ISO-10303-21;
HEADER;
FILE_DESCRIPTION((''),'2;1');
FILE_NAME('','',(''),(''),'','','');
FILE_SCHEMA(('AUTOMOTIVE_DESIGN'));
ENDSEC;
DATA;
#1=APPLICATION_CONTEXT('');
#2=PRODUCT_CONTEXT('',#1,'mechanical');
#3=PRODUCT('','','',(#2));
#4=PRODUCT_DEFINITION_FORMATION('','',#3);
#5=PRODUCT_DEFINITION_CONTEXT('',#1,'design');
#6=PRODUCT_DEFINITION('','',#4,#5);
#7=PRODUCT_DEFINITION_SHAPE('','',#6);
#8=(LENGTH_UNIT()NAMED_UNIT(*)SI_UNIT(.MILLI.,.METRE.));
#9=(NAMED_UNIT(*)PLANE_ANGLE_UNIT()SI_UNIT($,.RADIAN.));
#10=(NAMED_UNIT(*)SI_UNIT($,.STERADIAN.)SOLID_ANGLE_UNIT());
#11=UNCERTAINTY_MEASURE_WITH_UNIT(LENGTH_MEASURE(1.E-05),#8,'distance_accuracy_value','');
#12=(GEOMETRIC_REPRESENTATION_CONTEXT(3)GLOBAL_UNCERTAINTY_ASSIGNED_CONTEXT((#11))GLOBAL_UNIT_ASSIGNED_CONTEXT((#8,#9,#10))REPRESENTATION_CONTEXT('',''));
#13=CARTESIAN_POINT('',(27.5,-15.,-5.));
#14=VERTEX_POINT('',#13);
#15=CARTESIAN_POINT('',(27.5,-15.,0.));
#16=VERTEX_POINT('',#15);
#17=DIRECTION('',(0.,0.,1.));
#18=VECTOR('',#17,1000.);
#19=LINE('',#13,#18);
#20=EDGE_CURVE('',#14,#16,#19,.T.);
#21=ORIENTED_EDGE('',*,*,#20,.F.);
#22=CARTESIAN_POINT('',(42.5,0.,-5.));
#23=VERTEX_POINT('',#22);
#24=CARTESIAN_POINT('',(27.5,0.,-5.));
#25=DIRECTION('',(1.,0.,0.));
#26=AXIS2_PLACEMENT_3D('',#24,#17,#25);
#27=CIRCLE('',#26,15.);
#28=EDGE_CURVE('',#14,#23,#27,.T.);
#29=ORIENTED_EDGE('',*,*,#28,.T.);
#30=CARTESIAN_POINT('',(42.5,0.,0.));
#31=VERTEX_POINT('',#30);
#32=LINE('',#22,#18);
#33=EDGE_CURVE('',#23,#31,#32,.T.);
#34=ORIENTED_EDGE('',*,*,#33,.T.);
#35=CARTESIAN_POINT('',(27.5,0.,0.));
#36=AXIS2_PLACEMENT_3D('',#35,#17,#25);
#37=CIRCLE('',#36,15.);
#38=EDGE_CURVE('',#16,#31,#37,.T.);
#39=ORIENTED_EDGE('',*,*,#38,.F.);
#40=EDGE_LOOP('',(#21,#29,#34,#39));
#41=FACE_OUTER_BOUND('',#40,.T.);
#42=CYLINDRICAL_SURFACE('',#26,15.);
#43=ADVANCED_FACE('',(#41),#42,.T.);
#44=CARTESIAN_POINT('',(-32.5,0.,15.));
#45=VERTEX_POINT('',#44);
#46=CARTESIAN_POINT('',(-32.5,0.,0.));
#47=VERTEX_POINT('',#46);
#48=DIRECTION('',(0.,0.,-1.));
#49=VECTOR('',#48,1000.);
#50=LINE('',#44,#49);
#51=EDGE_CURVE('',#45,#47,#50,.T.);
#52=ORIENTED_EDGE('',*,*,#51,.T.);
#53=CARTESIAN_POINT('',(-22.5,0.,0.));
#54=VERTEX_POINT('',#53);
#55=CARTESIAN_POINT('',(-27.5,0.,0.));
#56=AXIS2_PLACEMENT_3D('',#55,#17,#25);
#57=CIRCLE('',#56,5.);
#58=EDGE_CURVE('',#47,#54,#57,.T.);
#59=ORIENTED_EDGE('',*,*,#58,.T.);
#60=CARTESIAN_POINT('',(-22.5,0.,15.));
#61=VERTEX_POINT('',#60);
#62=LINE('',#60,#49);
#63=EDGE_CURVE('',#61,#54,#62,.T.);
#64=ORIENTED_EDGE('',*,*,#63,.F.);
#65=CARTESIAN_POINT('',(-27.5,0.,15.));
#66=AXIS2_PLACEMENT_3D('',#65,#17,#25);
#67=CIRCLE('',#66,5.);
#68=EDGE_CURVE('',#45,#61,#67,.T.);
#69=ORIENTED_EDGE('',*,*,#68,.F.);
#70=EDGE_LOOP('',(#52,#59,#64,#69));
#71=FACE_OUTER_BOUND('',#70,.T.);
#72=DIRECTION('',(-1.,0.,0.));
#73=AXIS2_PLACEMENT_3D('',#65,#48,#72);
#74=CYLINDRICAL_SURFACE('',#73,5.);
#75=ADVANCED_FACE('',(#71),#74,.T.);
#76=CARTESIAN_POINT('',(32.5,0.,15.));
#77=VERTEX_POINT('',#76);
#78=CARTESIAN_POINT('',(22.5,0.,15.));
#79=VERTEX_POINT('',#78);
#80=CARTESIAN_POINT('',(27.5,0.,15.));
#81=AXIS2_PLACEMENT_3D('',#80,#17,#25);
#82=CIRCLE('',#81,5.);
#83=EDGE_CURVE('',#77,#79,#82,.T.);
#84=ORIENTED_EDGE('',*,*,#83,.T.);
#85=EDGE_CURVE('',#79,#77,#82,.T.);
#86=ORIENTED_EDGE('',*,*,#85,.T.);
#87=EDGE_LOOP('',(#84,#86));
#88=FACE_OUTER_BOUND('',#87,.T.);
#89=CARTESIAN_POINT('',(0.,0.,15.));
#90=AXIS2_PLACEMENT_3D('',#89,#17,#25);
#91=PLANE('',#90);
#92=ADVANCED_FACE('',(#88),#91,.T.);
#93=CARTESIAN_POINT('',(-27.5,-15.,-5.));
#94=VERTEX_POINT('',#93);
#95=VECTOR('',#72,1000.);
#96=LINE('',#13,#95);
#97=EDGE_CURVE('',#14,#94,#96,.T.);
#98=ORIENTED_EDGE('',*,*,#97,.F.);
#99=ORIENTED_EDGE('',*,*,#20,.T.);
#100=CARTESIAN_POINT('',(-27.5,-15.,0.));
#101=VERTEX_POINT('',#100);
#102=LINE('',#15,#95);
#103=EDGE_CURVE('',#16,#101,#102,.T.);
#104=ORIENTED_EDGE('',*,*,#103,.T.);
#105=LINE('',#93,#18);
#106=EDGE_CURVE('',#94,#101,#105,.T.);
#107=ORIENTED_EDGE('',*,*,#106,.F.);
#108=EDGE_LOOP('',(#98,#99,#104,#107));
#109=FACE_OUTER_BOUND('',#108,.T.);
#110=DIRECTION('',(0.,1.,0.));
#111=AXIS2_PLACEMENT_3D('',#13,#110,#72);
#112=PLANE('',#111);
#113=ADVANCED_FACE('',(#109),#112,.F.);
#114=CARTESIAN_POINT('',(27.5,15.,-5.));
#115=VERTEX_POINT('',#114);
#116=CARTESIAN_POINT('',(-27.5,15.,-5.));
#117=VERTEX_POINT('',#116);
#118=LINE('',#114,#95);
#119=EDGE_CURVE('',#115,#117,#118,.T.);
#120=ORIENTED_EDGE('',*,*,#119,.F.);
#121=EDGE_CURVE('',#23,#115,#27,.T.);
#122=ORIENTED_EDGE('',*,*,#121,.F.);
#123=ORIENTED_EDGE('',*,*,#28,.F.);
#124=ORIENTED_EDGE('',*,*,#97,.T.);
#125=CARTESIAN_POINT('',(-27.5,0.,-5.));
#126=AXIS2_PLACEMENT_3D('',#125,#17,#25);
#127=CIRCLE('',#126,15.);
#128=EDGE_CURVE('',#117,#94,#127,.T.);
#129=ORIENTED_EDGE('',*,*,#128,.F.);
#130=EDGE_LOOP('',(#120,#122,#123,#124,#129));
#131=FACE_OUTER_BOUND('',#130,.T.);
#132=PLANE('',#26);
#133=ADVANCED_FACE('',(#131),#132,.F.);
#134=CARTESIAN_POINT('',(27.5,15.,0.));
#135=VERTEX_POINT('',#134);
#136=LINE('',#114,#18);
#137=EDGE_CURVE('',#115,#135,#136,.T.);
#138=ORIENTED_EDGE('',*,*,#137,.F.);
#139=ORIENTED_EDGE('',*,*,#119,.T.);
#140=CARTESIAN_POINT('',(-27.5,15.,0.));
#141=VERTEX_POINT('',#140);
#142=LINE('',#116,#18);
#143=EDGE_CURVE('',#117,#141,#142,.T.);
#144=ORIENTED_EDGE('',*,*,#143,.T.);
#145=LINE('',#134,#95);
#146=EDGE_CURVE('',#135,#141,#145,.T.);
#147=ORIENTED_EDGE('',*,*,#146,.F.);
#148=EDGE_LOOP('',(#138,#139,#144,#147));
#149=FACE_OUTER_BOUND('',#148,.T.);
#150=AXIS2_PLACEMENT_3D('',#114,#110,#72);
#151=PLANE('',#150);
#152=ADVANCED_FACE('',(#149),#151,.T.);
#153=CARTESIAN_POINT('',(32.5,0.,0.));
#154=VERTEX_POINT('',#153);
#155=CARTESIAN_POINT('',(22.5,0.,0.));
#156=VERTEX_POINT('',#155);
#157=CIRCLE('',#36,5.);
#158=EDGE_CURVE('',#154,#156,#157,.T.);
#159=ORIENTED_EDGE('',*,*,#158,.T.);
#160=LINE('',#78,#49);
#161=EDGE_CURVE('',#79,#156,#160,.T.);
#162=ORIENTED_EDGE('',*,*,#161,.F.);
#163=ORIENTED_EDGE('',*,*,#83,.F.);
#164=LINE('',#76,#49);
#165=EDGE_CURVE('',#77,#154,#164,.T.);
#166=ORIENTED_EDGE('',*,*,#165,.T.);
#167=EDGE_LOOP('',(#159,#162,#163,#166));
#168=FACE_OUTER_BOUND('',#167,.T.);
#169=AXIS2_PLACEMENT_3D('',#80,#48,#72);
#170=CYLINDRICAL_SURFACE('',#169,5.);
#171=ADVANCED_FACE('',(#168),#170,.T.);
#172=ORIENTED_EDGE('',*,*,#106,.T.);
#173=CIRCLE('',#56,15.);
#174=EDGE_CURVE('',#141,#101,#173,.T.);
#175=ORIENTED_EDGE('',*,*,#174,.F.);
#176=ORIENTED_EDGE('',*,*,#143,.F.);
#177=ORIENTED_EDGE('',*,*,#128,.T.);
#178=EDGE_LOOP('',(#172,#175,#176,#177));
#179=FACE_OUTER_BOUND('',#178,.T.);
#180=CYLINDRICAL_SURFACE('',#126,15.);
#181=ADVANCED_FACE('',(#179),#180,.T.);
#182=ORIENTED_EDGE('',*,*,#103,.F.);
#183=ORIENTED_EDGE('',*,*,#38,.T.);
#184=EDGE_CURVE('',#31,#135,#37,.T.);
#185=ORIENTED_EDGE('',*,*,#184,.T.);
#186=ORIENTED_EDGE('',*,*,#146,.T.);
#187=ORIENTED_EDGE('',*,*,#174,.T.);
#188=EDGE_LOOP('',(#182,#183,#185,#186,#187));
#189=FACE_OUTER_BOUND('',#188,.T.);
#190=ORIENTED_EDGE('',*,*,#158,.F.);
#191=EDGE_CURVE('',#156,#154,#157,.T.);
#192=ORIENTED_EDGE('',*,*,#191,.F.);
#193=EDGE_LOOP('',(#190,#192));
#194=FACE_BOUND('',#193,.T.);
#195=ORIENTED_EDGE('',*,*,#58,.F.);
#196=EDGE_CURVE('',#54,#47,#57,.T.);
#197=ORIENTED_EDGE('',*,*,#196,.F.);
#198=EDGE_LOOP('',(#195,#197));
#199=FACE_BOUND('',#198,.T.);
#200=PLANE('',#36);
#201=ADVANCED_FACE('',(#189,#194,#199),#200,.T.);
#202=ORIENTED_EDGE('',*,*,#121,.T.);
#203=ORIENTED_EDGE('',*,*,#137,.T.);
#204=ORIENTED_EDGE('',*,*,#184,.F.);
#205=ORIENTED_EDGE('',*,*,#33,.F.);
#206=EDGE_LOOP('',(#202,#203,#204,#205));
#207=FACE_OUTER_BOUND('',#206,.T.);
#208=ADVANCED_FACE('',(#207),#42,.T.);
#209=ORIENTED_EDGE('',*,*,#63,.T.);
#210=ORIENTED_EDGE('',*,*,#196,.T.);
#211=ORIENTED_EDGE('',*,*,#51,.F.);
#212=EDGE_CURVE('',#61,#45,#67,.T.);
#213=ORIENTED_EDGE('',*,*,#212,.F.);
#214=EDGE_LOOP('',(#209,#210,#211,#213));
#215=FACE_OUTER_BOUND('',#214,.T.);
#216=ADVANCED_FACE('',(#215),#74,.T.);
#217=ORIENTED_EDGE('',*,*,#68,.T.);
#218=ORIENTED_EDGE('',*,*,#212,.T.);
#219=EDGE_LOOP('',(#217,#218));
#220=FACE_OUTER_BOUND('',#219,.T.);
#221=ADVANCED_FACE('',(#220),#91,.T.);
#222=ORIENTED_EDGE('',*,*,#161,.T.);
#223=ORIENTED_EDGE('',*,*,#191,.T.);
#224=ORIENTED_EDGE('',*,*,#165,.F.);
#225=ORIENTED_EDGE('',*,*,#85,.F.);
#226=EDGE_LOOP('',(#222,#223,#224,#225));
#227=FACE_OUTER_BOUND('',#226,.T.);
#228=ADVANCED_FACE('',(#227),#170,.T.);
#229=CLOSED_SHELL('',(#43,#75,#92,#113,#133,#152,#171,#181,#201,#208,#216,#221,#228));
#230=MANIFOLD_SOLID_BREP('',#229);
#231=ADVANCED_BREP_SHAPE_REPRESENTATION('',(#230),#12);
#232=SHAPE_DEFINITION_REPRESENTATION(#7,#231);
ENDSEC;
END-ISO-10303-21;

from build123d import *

# Parameters (mm, degrees)
LINK_PLATE_DEPTH = 5
SKETCH1_3_R      = 5
PINS_2X_10_DEPTH = 15


with BuildPart() as part:
    # Link Profile Sketch → Link Plate (new body)
    with BuildSketch(Plane.XY):
        with BuildLine():
            Line((27.5, -15), (-27.5, -15))
            ThreePointArc((-27.5, -15), (-42.5, 0), (-27.5, 15))
            Line((-27.5, 15), (27.5, 15))
            ThreePointArc((27.5, 15), (42.5, 0), (27.5, -15))
        make_face()
    extrude(amount=-LINK_PLATE_DEPTH)

    # Sketch1_3 → Pins 2x_10 (add)
    with BuildSketch(Plane.XY):
        with Locations((-27.5, 0)):
            Circle(SKETCH1_3_R)
        with Locations((27.5, 0)):
            Circle(SKETCH1_3_R)
    extrude(amount=PINS_2X_10_DEPTH)


solid = part.part
